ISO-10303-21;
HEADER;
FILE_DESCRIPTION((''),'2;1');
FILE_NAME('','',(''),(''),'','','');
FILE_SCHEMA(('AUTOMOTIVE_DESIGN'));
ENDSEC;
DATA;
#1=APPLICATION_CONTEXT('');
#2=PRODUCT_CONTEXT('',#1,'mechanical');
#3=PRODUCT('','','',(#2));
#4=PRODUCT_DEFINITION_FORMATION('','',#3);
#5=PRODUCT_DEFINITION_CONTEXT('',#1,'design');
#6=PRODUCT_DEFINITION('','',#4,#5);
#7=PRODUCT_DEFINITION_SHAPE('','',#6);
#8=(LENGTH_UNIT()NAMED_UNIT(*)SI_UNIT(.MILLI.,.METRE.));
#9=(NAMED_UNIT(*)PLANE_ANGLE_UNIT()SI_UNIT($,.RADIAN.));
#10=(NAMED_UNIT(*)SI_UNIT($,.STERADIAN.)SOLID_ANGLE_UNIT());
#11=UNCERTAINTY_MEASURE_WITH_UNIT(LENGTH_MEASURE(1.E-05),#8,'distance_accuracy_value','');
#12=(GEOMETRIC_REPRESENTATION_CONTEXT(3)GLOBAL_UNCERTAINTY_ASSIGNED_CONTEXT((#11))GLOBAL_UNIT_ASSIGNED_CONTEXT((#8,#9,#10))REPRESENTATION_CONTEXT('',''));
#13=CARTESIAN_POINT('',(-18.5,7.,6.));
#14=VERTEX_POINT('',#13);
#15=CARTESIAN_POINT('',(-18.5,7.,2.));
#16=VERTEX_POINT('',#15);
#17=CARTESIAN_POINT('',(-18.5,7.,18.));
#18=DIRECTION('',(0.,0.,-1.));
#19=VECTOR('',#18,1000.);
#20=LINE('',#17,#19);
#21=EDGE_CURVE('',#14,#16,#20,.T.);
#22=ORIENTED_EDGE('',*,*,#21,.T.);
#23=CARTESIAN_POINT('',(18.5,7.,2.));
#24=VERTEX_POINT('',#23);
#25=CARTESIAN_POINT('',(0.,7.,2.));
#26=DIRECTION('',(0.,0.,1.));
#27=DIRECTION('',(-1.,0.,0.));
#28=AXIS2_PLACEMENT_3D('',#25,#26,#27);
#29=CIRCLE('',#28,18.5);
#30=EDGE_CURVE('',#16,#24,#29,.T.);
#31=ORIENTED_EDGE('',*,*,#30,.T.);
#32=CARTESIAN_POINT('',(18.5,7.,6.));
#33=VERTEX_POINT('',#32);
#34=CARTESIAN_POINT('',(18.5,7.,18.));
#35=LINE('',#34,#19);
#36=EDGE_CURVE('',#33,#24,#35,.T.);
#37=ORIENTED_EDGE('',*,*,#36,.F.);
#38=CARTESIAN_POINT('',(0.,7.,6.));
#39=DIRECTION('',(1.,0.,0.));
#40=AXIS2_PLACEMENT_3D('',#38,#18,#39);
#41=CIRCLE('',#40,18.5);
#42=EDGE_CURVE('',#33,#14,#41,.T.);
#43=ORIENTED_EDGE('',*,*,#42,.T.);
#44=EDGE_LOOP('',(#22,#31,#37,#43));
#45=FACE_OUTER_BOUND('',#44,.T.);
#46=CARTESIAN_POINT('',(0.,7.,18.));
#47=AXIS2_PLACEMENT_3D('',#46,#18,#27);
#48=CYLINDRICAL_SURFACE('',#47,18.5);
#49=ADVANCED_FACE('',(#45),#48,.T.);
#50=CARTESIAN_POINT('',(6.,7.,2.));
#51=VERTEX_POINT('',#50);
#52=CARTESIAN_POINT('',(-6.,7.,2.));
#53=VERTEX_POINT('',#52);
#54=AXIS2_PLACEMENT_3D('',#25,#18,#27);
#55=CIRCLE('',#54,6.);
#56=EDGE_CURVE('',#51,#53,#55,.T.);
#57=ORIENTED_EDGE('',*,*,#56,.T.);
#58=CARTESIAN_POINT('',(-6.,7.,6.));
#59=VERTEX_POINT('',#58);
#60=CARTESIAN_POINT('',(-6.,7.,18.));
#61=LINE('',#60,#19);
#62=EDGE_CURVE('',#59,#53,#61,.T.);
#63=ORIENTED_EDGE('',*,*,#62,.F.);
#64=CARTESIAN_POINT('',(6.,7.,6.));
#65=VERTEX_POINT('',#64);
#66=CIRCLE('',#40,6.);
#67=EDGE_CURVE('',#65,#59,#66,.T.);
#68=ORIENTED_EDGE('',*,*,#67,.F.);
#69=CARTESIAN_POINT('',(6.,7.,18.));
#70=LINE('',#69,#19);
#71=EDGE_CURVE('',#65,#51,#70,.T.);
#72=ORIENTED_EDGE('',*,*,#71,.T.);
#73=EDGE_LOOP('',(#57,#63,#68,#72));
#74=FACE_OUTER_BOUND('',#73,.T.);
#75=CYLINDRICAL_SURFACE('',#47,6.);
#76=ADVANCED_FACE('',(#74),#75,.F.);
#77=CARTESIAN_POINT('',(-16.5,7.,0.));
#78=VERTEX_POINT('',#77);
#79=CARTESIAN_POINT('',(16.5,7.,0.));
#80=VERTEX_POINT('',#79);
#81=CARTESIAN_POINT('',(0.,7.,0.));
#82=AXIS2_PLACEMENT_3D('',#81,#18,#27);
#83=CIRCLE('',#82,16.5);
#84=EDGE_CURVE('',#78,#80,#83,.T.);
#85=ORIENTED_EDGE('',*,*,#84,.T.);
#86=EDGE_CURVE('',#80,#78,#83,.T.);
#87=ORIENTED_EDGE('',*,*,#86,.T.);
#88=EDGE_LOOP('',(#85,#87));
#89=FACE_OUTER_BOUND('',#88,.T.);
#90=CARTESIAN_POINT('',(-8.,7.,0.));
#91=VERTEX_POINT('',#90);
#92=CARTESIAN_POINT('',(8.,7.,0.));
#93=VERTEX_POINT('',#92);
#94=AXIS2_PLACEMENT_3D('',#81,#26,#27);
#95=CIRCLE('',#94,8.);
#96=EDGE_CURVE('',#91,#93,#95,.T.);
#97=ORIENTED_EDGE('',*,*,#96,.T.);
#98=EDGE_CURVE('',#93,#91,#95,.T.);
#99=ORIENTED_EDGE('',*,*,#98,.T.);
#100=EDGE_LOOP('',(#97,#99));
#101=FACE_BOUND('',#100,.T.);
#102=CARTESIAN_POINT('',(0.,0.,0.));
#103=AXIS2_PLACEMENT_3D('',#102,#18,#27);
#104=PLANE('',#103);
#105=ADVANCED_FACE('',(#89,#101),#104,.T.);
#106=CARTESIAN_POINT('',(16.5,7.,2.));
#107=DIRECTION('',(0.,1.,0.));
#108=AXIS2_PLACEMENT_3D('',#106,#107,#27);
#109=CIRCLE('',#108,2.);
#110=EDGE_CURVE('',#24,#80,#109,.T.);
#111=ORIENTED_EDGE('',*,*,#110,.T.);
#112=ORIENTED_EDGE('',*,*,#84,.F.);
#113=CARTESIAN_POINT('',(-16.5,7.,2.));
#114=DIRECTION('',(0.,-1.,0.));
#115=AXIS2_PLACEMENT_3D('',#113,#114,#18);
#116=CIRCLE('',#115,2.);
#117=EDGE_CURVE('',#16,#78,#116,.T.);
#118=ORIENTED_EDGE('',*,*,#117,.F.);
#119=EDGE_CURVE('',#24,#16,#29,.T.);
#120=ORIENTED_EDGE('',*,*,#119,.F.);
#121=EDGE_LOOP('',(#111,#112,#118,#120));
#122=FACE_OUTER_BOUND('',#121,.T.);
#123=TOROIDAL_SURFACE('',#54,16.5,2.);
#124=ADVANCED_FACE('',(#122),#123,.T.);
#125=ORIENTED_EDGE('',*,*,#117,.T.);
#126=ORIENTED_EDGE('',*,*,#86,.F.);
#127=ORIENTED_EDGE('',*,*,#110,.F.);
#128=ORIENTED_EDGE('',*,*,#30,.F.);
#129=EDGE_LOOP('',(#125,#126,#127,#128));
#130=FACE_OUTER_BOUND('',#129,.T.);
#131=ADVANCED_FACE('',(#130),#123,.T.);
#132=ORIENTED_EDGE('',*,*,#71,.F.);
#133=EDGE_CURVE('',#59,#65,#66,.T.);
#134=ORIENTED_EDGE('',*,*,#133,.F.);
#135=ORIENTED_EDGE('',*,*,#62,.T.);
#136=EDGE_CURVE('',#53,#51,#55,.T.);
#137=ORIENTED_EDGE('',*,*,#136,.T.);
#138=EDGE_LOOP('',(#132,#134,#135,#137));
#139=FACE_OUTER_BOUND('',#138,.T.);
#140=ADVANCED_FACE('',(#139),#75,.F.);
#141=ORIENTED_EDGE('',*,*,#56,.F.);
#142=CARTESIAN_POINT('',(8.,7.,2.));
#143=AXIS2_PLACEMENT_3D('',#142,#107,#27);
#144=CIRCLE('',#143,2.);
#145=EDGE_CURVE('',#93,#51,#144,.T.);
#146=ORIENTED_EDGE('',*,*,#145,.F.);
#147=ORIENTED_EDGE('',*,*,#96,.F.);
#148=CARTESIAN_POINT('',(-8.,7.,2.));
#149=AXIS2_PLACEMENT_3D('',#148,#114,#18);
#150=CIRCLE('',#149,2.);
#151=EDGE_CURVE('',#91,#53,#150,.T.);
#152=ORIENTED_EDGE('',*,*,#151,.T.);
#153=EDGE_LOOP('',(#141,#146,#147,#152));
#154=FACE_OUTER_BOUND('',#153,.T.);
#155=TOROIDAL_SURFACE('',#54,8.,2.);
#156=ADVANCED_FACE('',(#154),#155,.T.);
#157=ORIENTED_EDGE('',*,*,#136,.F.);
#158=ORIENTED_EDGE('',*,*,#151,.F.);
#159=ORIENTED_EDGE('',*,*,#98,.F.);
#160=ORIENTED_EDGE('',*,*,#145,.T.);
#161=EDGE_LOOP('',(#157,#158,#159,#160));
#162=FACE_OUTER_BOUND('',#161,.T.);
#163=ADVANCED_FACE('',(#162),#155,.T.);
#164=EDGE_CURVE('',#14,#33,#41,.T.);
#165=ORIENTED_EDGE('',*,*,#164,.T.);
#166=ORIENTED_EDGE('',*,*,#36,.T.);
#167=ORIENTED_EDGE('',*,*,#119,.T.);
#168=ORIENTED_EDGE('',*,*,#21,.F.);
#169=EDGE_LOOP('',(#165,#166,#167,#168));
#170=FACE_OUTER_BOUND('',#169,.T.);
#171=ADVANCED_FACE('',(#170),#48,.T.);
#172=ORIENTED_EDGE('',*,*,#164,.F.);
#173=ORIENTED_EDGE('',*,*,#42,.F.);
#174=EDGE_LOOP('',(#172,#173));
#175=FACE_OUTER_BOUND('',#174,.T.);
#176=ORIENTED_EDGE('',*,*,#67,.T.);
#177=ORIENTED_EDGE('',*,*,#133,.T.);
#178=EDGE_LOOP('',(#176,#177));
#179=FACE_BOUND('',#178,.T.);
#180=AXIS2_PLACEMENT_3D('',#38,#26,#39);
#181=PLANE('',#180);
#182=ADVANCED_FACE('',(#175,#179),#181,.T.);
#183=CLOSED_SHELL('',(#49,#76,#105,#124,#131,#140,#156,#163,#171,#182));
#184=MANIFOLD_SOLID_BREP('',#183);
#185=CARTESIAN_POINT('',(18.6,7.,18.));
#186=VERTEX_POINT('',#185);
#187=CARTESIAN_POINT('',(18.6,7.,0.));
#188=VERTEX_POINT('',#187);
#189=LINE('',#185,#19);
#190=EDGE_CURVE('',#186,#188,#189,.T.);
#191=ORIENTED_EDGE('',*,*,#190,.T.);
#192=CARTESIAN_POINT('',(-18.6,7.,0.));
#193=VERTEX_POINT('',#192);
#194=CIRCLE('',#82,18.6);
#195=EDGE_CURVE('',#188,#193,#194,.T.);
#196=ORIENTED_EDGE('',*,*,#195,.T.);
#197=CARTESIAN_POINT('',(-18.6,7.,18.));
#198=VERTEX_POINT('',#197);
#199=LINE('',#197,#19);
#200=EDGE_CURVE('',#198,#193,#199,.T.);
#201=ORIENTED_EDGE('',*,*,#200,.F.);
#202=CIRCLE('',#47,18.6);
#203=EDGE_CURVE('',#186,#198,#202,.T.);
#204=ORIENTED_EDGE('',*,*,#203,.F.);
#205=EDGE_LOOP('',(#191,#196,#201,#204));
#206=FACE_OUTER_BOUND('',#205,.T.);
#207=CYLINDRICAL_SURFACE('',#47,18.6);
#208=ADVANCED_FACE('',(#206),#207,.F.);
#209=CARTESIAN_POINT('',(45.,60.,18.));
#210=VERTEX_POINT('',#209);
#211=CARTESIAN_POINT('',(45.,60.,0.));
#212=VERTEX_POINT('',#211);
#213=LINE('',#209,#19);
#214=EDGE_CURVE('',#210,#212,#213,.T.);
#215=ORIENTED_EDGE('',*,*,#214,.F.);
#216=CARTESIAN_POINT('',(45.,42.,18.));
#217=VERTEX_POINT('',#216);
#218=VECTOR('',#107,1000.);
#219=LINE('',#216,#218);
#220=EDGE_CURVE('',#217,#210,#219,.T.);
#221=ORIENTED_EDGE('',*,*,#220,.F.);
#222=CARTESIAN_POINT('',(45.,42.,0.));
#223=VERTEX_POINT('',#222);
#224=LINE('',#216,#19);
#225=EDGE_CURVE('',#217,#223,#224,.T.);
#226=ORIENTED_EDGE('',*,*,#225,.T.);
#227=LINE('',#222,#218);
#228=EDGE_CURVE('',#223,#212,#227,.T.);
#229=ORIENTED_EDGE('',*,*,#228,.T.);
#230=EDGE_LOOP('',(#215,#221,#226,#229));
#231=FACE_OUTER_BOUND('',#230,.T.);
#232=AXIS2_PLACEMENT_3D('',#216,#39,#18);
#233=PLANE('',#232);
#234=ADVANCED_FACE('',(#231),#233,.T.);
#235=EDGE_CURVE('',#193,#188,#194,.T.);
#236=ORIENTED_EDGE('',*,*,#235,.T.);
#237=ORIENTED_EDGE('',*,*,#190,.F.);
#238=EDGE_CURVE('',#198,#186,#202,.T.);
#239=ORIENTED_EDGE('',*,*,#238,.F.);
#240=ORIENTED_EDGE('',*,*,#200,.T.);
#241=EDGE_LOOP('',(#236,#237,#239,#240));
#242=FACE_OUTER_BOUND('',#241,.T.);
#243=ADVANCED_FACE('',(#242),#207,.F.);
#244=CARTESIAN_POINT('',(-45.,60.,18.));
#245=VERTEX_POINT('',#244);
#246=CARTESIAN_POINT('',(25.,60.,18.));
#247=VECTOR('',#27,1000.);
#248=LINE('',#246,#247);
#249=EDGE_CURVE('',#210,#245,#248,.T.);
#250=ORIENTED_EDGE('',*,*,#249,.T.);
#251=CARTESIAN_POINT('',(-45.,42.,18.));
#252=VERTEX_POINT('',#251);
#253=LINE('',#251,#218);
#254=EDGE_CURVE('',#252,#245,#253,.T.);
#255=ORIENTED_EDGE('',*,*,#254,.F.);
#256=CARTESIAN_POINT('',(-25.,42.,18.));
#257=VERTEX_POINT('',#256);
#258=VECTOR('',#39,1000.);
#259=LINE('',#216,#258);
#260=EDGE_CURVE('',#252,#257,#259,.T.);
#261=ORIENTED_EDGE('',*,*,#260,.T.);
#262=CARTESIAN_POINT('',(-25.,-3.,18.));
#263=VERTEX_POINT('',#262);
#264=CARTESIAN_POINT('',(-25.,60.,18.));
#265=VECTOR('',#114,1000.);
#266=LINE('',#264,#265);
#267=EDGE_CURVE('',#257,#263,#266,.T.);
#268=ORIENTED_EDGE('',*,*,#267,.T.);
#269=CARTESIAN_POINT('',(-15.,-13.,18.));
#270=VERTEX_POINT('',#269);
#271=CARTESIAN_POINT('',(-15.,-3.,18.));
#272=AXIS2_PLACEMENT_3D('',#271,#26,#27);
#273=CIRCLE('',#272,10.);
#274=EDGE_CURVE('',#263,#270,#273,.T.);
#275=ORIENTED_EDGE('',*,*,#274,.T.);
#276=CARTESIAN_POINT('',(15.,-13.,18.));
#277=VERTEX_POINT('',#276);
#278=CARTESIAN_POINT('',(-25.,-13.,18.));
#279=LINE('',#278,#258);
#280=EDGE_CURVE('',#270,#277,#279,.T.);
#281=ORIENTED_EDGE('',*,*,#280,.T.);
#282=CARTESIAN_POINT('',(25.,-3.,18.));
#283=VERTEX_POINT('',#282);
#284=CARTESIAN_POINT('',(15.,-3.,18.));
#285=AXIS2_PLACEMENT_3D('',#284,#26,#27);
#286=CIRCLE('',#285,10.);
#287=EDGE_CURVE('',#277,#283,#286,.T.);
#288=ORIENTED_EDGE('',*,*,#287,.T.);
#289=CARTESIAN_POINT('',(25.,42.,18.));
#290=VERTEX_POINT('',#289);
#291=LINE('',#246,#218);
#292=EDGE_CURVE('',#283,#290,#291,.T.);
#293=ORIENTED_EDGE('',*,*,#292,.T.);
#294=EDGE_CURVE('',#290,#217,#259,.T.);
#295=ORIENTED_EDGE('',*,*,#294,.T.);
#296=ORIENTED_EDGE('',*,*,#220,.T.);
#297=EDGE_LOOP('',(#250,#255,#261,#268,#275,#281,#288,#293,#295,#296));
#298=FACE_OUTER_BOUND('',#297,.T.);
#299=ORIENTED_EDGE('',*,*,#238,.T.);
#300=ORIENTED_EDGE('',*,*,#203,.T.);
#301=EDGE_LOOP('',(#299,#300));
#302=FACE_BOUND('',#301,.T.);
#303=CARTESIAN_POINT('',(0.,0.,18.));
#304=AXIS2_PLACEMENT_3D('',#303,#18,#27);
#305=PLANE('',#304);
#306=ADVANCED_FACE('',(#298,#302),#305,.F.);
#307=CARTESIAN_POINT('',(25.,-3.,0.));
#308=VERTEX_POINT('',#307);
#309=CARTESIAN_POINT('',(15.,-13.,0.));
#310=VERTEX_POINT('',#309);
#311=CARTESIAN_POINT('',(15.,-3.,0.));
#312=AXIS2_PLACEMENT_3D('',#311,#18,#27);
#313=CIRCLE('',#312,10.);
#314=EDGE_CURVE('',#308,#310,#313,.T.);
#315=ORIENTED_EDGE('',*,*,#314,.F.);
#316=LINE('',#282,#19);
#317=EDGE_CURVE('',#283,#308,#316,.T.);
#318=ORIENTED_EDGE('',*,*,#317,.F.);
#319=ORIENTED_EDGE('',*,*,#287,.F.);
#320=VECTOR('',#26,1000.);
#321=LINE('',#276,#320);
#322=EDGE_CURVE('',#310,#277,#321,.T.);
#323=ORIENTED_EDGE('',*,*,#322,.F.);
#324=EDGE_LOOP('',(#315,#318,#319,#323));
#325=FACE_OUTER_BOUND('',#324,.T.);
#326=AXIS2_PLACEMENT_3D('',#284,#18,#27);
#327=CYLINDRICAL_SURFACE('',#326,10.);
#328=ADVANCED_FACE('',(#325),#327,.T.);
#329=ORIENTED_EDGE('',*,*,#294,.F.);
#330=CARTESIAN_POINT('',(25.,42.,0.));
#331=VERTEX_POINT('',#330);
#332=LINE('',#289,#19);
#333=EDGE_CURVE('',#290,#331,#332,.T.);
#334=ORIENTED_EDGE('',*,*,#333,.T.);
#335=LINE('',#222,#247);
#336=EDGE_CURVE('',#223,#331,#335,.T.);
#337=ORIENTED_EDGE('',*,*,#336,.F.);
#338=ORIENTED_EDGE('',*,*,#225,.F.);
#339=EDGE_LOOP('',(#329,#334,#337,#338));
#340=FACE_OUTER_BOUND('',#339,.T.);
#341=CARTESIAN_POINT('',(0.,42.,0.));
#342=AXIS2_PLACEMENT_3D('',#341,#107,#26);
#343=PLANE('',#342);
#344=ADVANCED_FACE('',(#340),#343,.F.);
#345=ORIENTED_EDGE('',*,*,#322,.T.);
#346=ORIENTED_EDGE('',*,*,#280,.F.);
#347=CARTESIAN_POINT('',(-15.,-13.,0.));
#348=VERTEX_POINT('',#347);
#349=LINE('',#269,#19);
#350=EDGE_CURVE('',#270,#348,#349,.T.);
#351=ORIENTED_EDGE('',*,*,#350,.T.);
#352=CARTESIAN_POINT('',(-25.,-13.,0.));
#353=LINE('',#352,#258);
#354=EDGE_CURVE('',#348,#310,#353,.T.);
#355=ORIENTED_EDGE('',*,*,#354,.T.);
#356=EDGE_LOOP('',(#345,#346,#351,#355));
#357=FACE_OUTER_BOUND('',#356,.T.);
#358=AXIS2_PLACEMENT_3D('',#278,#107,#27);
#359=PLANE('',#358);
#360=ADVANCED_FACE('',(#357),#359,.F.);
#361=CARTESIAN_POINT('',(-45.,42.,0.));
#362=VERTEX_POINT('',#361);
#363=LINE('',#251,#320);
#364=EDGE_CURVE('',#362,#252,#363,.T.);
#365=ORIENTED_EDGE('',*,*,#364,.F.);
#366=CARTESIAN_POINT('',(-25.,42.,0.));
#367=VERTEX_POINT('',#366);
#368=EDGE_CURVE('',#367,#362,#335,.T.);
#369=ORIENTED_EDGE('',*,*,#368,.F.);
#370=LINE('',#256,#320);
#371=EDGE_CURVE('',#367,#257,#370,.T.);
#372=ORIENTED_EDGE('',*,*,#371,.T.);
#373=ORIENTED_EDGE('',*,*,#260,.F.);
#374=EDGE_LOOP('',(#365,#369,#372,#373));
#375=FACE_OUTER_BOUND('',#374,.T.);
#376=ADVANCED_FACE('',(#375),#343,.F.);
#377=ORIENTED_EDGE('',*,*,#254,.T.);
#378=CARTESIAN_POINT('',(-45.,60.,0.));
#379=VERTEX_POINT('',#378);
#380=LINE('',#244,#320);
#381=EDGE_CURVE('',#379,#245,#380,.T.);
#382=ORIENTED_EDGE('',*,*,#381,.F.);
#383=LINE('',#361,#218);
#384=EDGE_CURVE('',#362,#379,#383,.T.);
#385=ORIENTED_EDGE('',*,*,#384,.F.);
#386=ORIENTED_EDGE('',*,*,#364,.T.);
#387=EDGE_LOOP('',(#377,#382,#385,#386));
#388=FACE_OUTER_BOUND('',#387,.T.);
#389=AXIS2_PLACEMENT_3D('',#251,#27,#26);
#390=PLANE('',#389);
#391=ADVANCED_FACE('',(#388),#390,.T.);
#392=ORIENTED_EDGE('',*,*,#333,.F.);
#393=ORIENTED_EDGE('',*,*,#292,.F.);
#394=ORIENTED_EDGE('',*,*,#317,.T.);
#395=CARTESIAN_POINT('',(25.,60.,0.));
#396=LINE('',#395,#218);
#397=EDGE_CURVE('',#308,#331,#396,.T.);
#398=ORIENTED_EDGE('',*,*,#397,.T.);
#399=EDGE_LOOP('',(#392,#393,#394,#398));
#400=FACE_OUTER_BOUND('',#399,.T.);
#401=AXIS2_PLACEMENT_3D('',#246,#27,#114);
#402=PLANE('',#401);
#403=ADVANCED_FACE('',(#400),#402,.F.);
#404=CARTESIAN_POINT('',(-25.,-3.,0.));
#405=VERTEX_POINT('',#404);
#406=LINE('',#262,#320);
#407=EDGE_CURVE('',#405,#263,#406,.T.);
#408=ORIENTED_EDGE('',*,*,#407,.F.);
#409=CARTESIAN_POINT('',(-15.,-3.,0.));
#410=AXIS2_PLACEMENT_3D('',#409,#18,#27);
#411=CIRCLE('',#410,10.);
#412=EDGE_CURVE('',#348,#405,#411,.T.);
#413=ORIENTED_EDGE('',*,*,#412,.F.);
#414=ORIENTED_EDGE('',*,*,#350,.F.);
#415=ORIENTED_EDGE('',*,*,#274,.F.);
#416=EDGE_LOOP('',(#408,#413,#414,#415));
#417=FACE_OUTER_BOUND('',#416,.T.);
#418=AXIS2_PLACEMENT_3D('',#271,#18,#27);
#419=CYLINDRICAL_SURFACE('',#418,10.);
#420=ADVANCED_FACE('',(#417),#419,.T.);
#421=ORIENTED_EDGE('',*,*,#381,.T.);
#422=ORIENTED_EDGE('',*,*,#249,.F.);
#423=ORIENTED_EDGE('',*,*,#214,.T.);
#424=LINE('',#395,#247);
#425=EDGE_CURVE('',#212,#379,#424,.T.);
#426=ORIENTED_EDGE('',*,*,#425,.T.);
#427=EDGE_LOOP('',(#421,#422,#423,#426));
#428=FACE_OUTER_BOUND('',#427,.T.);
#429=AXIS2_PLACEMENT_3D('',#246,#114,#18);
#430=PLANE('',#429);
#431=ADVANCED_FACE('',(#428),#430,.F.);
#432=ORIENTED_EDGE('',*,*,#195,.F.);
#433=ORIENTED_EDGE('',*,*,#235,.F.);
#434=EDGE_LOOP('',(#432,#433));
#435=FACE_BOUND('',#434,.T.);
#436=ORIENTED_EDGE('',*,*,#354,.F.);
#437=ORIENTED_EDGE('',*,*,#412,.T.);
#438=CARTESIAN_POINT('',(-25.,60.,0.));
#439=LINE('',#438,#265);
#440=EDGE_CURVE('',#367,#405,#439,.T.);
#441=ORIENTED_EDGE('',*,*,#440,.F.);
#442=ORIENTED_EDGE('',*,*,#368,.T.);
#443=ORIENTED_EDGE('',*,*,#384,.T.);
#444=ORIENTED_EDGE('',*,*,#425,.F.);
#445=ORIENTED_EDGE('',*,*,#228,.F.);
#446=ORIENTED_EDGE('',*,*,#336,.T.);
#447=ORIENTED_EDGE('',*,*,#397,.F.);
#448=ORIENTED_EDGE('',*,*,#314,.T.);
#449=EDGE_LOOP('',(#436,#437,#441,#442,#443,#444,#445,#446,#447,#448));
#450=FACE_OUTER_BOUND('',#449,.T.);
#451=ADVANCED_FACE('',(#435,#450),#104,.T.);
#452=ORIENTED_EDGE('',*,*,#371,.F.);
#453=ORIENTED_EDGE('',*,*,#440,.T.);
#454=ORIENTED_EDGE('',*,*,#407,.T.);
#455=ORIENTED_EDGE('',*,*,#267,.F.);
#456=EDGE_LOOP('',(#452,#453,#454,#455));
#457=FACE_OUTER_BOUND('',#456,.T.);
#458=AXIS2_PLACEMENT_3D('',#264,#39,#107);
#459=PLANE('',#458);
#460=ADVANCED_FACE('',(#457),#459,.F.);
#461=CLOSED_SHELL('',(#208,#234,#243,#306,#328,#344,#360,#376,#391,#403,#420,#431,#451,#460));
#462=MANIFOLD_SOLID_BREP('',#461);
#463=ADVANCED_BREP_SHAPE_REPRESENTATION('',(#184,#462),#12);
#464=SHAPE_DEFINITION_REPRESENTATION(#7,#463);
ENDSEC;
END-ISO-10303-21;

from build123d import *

# Parameters (mm, degrees)
SKETCH_1_W             = 50
SKETCH_1_H             = 120
EXTRUDE_1_DEPTH        = 18
SKETCH_2_W             = 90
SKETCH_2_H             = 18
EXTRUDE_2_DEPTH        = 18
FILLET_1_R             = 10
SKETCH_3_R             = 6
CUT_EXTRUDE_1_DEPTH    = 78.129760793
SKETCH_4_R             = 18.6
SKETCH_4_R_2           = 18.5
CUT_EXTRUDE_2_DEPTH    = 78.129760793
PATTERN_LINEAR_1_COUNT = 2
PATTERN_LINEAR_1_PITCH = 47
FILLET_2_R             = 2
FILLET_3_R             = 2
SKETCH_5_W             = 55.708110293
SKETCH_5_H             = 48.006779115
CUT_EXTRUDE_3_DEPTH    = 78.129760793
FILLET_4_R             = 10
SKETCH_6_R             = 18.6
CUT_EXTRUDE_4_DEPTH    = 12


with BuildPart() as part:
    # 草图1 → 凸台-拉伸1 (new body)
    with BuildSketch(Plane.XY):
        Rectangle(SKETCH_1_W, SKETCH_1_H)
    extrude(amount=EXTRUDE_1_DEPTH)

    # 草图2 → 凸台-拉伸2 (add)
    with BuildSketch(Plane(origin=(0, 60, 0), x_dir=(1, 0, 0), z_dir=(0, 1, 0))):
        with Locations((0, -9)):
            Rectangle(SKETCH_2_W, SKETCH_2_H)
    extrude(amount=-EXTRUDE_2_DEPTH)

    # 圆角1
    fillet_1_edges = [part.edges().sort_by_distance(p)[0] for p in [
        (25, -60, 9),
        (-25, -60, 9),
    ]]
    fillet(fillet_1_edges, radius=FILLET_1_R)

    # 草图3 → 切除-拉伸1 (cut, through all)
    with BuildSketch(Plane(origin=(0, 0, 0), x_dir=(-1, 0, 0), z_dir=(0, 0, -1))):
        with Locations((0, -40)):
            Circle(SKETCH_3_R)
    cut_extrude_1 = extrude(amount=-CUT_EXTRUDE_1_DEPTH, mode=Mode.SUBTRACT)

    # 草图4 → 切除-拉伸2 (cut, through all)
    with BuildSketch(Plane(origin=(0, 0, 0), x_dir=(-1, 0, 0), z_dir=(0, 0, -1))):
        with Locations((0, -40)):
            Circle(SKETCH_4_R)
        with Locations((0, -40)):
            Circle(SKETCH_4_R_2, mode=Mode.SUBTRACT)
    cut_extrude_2 = extrude(amount=-CUT_EXTRUDE_2_DEPTH, mode=Mode.SUBTRACT)


with BuildPart() as cut_extrude_2_piece_1:
    # of the separate pieces the step leaves, piece 1, a body of its own (cut_extrude_2_pieces)
    add(part.part.solids().sort_by_distance((-25, -50, 0))[0])

    # 阵列(线性)1: 切除-拉伸1, 切除-拉伸2 ×2
    with Locations(*[(0, i * PATTERN_LINEAR_1_PITCH, 0) for i in range(1, PATTERN_LINEAR_1_COUNT)]):
        add(cut_extrude_1, mode=Mode.SUBTRACT)
        add(cut_extrude_2, mode=Mode.SUBTRACT)

    # 圆角3
    fillet_3_edges = [cut_extrude_2_piece_1.edges().sort_by_distance(p)[0] for p in [
        (6, 7, 18),
        (6, 7, 0),
        (18.5, 7, 18),
        (18.5, 7, 0),
    ]]
    fillet(fillet_3_edges, radius=FILLET_3_R)


with BuildPart() as cut_extrude_2_piece_2:
    # of the separate pieces the step leaves, piece 2, a body of its own (cut_extrude_2_pieces)
    add(part.part.solids().sort_by_distance((-18.5, -40, 0))[0])

    # 圆角2
    fillet_2_edges = [cut_extrude_2_piece_2.edges().sort_by_distance(p)[0] for p in [
        (6, -40, 18),
        (6, -40, 0),
        (18.5, -40, 18),
        (18.5, -40, 0),
    ]]
    fillet(fillet_2_edges, radius=FILLET_2_R)


with BuildPart() as cut_extrude_3_tool:
    # 草图5 → 切除-拉伸3 (new, through all)
    with BuildSketch(Plane(origin=(0, 0, 0), x_dir=(-1, 0, 0), z_dir=(0, 0, -1))):
        with Locations((-2.854055147, -37.003389558)):
            Rectangle(SKETCH_5_W, SKETCH_5_H)
    extrude(amount=-CUT_EXTRUDE_3_DEPTH)


with BuildPart() as cut_extrude_2_piece_1_1:
    add(cut_extrude_2_piece_1.part)

    # 切除-拉伸3: cut by cut_extrude_3_tool
    add(cut_extrude_3_tool.part, mode=Mode.SUBTRACT)

    # 圆角4
    fillet_4_edges = [cut_extrude_2_piece_1_1.edges().sort_by_distance(p)[0] for p in [
        (25, -13, 9),
        (-25, -13, 9),
    ]]
    fillet(fillet_4_edges, radius=FILLET_4_R)

    # 草图6 → 切除-拉伸4 (cut)
    with BuildSketch(Plane.XY.offset(18)):
        with Locations(Location((0, 7, 0), (0, 0, 180))):
            Circle(SKETCH_6_R)
    extrude(amount=-CUT_EXTRUDE_4_DEPTH, mode=Mode.SUBTRACT)


with BuildPart() as cut_extrude_2_piece_2_1:
    add(cut_extrude_2_piece_2.part)

    # 切除-拉伸3: cut by cut_extrude_3_tool
    add(cut_extrude_3_tool.part, mode=Mode.SUBTRACT)


solid = cut_extrude_2_piece_1_1.part
